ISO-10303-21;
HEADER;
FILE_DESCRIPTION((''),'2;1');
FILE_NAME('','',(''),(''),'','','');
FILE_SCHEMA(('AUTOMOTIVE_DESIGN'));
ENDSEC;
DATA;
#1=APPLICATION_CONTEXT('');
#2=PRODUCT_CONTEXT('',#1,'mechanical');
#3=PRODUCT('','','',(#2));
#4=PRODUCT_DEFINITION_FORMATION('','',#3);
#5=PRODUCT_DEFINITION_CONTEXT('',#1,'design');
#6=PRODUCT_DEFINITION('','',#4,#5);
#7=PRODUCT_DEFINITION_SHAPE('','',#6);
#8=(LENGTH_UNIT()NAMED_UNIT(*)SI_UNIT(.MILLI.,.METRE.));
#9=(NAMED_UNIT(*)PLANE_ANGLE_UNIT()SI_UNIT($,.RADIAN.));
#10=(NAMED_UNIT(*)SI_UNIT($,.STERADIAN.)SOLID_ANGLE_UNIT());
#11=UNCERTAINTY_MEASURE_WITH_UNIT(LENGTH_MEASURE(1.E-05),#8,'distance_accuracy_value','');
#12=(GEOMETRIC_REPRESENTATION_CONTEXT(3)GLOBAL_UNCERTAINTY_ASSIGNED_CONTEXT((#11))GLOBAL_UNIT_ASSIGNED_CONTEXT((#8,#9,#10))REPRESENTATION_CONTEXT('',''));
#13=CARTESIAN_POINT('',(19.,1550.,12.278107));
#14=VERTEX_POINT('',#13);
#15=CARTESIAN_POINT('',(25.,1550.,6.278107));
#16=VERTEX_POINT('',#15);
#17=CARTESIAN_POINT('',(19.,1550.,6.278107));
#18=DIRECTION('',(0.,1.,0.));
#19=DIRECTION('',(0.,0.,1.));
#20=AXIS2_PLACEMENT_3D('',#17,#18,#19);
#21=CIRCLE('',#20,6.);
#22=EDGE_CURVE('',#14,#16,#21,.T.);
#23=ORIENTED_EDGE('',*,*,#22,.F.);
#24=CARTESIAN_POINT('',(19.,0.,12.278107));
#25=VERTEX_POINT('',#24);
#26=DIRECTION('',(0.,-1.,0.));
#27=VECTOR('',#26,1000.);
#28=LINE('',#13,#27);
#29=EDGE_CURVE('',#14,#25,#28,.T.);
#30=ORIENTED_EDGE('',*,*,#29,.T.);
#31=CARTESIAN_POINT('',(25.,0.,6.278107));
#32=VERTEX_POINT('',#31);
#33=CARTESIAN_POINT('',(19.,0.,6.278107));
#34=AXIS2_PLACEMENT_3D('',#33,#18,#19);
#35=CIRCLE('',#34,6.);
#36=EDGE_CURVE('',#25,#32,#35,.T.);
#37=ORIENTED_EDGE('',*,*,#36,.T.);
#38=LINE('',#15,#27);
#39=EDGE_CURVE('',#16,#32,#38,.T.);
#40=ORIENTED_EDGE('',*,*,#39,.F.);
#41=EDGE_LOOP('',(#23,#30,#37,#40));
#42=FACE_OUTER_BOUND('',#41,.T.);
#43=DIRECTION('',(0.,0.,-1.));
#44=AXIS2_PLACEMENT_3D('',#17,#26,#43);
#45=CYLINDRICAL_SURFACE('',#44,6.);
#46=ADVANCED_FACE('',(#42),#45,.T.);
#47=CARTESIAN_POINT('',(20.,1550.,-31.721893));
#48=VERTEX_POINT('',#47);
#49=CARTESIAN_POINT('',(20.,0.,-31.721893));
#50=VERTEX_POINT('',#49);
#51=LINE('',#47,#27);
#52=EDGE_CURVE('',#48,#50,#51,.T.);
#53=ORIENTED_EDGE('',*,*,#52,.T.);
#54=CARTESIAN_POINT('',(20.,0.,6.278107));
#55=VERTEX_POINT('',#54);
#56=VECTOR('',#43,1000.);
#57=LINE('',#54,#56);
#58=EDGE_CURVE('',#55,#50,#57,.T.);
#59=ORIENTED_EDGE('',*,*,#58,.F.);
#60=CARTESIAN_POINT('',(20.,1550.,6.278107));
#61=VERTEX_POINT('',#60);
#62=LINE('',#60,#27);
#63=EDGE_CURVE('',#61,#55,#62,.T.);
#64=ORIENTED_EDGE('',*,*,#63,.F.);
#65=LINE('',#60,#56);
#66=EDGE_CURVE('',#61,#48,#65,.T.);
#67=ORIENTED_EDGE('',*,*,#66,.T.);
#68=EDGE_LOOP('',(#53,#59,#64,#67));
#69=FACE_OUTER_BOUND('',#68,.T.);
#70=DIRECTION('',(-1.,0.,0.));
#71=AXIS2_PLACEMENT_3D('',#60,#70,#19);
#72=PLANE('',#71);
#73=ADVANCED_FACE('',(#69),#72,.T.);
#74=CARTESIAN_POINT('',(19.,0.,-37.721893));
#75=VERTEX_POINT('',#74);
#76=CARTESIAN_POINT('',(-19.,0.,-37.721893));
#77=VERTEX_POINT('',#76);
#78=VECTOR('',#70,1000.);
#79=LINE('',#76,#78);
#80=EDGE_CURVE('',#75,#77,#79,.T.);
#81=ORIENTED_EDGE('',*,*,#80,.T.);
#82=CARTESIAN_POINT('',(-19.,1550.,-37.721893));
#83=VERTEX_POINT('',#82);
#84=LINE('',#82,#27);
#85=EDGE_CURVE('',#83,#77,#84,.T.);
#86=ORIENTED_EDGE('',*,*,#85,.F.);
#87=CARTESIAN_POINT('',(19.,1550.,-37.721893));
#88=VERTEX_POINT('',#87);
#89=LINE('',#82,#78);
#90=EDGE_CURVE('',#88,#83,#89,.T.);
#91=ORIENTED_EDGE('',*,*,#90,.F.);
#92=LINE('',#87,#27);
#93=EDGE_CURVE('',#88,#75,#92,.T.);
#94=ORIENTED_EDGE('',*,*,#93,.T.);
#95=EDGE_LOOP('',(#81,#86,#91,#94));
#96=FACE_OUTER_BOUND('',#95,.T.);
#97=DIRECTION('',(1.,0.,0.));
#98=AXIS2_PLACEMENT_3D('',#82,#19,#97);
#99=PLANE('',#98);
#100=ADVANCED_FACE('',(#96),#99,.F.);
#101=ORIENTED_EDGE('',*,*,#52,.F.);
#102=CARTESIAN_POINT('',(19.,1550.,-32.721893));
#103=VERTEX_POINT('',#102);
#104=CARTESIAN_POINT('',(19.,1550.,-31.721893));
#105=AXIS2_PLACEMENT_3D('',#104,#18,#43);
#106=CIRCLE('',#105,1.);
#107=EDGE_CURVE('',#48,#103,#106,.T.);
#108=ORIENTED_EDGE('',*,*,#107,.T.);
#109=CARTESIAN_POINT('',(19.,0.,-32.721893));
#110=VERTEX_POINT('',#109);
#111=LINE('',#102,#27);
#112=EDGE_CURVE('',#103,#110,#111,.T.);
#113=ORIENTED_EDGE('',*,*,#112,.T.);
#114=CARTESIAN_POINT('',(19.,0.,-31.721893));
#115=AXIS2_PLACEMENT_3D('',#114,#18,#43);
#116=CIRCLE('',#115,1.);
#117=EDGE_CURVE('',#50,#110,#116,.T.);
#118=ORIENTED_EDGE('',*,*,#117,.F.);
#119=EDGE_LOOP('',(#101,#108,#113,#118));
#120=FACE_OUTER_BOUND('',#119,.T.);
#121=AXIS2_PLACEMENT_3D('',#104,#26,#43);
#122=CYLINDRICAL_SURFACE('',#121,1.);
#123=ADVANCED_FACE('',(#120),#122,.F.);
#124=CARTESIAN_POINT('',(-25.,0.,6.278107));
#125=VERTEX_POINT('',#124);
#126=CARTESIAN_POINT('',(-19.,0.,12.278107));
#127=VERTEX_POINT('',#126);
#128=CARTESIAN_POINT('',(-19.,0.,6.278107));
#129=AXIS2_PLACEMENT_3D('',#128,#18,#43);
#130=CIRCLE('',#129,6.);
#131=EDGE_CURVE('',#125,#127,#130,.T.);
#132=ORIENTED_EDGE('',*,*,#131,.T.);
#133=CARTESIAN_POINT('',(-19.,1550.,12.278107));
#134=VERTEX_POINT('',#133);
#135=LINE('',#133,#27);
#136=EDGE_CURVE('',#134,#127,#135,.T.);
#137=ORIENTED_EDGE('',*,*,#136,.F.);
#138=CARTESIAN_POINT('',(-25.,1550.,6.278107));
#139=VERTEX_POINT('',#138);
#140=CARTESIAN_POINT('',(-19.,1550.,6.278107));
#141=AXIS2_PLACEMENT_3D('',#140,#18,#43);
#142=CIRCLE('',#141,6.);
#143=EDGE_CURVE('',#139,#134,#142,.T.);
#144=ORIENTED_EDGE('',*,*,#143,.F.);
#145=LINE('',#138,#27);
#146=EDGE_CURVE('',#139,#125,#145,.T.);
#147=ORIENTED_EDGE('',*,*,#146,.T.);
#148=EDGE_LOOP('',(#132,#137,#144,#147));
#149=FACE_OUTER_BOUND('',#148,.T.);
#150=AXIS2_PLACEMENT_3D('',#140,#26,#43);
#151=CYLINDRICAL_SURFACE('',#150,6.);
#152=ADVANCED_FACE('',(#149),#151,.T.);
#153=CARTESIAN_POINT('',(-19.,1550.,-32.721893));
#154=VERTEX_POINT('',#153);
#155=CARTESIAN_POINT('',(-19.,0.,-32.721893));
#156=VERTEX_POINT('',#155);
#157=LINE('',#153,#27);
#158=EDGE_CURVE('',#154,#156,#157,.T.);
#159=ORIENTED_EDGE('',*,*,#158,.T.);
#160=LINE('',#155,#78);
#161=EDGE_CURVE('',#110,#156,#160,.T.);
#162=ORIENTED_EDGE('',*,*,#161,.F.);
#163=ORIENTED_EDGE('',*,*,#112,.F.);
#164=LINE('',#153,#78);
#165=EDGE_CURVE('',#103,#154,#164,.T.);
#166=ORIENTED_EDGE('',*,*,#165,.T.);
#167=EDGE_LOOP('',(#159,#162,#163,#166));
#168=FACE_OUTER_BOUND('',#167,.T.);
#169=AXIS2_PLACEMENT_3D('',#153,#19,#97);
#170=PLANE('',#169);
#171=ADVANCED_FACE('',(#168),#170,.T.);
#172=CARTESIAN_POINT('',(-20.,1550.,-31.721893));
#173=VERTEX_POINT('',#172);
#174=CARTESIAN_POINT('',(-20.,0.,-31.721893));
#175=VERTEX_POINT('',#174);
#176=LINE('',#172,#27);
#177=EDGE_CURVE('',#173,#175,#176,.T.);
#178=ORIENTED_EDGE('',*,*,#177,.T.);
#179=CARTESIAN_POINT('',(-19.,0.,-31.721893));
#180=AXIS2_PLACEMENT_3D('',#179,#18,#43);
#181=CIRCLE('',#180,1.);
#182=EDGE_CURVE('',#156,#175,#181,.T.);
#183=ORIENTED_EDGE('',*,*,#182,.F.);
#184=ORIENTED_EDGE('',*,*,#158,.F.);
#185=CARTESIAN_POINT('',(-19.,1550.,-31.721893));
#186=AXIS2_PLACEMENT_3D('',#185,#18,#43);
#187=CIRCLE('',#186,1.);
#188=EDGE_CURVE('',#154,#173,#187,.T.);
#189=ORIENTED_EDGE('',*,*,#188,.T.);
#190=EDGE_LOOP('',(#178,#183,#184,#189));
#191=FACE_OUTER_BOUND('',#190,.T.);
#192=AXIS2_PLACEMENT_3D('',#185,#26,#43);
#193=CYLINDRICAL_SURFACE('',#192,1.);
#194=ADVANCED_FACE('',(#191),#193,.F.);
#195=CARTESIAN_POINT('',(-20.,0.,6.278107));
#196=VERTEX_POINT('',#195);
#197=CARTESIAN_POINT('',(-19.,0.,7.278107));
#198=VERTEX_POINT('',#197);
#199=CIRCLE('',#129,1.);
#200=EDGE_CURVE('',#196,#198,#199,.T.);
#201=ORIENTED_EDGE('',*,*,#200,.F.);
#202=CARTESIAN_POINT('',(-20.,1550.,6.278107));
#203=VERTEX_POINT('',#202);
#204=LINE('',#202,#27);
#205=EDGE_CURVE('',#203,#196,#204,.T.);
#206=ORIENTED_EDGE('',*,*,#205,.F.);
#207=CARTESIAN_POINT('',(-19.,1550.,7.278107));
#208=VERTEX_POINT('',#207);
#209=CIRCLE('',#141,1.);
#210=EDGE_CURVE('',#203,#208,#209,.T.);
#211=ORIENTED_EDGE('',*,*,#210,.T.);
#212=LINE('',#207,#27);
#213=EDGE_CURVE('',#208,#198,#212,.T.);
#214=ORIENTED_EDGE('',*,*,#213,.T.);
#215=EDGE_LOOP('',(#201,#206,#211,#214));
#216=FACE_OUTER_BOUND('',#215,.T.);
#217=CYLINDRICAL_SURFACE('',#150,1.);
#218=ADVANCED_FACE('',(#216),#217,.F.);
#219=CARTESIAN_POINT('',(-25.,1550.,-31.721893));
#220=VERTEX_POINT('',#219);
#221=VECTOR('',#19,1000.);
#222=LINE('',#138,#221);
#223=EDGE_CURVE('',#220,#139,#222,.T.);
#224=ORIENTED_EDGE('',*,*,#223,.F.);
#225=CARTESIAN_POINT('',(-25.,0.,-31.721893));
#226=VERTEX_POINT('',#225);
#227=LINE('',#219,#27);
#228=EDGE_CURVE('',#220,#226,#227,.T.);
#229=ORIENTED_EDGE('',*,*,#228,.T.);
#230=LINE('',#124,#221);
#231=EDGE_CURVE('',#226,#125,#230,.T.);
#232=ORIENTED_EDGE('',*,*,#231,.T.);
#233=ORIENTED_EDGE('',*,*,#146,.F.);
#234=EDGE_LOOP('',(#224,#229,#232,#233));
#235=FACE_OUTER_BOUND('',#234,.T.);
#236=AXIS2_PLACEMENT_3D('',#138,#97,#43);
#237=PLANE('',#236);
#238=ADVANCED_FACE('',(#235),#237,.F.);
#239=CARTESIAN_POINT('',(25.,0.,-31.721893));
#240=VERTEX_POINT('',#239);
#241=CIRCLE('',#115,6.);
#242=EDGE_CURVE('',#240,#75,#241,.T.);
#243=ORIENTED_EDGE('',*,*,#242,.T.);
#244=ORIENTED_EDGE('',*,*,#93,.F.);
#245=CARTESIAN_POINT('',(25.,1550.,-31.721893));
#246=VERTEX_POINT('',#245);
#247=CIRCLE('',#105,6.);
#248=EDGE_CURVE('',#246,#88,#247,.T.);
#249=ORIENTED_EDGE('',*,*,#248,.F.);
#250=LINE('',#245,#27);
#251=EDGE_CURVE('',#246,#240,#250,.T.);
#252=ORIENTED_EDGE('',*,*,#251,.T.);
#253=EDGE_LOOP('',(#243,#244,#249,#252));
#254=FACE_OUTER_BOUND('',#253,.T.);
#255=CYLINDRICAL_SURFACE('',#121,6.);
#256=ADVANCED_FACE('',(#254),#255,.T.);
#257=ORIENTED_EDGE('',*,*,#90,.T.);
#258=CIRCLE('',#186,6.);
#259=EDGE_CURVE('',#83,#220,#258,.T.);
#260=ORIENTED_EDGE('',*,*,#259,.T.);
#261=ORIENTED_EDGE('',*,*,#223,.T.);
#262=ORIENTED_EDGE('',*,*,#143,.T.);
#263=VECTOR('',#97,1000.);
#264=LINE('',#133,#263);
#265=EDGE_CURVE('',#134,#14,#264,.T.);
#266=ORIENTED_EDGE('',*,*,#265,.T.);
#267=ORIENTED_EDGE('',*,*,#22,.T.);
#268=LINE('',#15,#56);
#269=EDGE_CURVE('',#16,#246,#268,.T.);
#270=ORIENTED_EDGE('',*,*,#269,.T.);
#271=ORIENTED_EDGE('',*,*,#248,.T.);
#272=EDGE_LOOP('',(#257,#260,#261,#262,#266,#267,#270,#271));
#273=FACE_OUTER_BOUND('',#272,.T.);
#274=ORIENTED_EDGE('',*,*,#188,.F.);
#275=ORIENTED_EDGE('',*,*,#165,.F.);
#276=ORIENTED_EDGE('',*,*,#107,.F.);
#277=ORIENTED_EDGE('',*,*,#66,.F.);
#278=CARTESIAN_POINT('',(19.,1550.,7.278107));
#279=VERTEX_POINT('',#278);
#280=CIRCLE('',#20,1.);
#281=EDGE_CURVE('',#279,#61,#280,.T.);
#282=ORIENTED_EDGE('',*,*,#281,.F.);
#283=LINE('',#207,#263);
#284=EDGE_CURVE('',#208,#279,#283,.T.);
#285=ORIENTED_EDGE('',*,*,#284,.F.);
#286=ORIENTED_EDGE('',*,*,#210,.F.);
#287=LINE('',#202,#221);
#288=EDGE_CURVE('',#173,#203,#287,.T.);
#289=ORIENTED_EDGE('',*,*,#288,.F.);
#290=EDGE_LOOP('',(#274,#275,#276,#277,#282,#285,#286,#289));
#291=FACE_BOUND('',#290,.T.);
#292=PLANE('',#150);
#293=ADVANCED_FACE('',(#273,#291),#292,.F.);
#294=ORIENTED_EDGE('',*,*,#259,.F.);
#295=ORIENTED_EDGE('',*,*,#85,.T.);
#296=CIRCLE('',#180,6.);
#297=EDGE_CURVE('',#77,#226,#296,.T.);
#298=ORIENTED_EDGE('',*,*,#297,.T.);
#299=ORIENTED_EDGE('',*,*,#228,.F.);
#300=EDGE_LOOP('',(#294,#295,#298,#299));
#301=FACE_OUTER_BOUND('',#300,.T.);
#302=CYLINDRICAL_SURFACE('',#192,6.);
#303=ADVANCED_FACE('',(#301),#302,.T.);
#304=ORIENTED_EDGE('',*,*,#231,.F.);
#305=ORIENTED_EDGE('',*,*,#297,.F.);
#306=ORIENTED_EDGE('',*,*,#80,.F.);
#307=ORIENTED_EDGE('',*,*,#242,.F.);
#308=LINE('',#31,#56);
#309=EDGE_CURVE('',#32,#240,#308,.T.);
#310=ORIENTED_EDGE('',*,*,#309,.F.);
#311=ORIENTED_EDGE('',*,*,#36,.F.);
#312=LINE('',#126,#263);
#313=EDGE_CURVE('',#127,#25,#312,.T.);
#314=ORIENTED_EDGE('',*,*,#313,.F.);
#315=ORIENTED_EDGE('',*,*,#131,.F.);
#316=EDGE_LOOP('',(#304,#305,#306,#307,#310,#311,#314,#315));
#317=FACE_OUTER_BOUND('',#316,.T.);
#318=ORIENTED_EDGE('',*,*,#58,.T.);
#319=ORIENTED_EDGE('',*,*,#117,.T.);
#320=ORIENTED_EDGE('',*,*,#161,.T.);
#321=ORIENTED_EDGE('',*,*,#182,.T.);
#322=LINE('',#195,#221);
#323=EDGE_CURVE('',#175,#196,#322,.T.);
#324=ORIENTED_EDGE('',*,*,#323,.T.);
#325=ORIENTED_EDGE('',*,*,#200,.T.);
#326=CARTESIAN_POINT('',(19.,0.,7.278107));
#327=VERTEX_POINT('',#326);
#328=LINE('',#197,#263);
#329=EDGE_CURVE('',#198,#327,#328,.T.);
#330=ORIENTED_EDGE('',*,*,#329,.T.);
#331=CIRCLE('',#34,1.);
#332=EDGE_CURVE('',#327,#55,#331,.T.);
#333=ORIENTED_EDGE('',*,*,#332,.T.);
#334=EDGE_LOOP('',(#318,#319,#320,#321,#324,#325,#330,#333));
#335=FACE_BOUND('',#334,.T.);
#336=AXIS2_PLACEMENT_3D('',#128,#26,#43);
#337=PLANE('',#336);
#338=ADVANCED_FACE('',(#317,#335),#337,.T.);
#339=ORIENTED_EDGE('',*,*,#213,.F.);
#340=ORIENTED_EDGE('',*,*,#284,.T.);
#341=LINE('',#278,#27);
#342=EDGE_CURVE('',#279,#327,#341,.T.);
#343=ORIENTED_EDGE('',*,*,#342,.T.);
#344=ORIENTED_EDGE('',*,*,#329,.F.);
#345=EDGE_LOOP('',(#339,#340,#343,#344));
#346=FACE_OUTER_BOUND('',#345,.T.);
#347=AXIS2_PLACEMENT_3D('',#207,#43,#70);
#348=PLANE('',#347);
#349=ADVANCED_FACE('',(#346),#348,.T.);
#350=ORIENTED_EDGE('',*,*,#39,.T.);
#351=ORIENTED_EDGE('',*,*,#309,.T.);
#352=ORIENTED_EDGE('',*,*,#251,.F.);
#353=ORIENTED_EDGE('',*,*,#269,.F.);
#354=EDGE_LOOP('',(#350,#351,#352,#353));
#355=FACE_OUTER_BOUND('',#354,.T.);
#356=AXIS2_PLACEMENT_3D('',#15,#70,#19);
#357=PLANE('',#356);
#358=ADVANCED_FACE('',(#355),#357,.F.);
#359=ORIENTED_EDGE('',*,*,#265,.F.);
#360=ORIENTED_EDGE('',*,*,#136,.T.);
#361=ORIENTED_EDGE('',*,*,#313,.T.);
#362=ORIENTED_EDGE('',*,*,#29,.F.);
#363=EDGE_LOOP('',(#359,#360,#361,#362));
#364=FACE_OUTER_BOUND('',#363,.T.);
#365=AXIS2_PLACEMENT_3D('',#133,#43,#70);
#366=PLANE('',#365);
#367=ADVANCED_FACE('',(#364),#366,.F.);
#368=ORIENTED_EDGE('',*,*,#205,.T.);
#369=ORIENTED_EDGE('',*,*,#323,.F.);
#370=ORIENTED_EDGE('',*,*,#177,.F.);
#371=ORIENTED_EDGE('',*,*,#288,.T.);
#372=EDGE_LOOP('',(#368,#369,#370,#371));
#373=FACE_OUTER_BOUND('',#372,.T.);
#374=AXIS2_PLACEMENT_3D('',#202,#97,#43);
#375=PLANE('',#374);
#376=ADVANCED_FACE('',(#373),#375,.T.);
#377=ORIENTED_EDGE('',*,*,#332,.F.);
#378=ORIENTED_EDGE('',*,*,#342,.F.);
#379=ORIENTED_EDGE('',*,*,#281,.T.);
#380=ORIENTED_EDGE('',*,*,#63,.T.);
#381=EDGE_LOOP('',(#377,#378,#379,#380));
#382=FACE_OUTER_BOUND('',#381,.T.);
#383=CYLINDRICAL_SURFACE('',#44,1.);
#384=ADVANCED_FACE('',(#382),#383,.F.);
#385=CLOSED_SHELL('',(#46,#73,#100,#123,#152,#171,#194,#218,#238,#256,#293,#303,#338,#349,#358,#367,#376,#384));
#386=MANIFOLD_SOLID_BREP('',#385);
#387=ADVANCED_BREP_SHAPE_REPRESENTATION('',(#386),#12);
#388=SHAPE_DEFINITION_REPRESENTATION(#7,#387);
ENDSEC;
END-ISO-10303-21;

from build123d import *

# Parameters (mm, degrees)
EXTRUDE_1_DEPTH = 1550


with BuildPart() as part:
    # 草图1 → 凸台-拉伸1 (new body)
    with BuildSketch(Plane(origin=(0, 0, 0), x_dir=(1, 0, 0), z_dir=(0, 1, 0))):
        with BuildLine():
            Line((-19, -12.278106509), (19, -12.278106509))
            ThreePointArc((19, -12.278106509), (23.242640687, -10.520747196), (25, -6.278106509))
            Line((25, -6.278106509), (25, 31.721893491))
            ThreePointArc((25, 31.721893491), (23.242640687, 35.964534178), (19, 37.721893491))
            Line((19, 37.721893491), (-19, 37.721893491))
            ThreePointArc((-19, 37.721893491), (-23.242640687, 35.964534178), (-25, 31.721893491))
            Line((-25, 31.721893491), (-25, -6.278106509))
            ThreePointArc((-25, -6.278106509), (-23.242640687, -10.520747196), (-19, -12.278106509))
        make_face()
        with BuildLine():
            Line((-19, -7.278106509), (19, -7.278106509))
            ThreePointArc((19, -7.278106509), (19.707106781, -6.98521329), (20, -6.278106509))
            Line((20, -6.278106509), (20, 31.721893491))
            ThreePointArc((20, 31.721893491), (19.707106781, 32.429000272), (19, 32.721893491))
            Line((19, 32.721893491), (-19, 32.721893491))
            ThreePointArc((-19, 32.721893491), (-19.707106781, 32.429000272), (-20, 31.721893491))
            Line((-20, 31.721893491), (-20, -6.278106509))
            ThreePointArc((-20, -6.278106509), (-19.707106781, -6.98521329), (-19, -7.278106509))
        make_face(mode=Mode.SUBTRACT)
    extrude(amount=EXTRUDE_1_DEPTH)


solid = part.part
